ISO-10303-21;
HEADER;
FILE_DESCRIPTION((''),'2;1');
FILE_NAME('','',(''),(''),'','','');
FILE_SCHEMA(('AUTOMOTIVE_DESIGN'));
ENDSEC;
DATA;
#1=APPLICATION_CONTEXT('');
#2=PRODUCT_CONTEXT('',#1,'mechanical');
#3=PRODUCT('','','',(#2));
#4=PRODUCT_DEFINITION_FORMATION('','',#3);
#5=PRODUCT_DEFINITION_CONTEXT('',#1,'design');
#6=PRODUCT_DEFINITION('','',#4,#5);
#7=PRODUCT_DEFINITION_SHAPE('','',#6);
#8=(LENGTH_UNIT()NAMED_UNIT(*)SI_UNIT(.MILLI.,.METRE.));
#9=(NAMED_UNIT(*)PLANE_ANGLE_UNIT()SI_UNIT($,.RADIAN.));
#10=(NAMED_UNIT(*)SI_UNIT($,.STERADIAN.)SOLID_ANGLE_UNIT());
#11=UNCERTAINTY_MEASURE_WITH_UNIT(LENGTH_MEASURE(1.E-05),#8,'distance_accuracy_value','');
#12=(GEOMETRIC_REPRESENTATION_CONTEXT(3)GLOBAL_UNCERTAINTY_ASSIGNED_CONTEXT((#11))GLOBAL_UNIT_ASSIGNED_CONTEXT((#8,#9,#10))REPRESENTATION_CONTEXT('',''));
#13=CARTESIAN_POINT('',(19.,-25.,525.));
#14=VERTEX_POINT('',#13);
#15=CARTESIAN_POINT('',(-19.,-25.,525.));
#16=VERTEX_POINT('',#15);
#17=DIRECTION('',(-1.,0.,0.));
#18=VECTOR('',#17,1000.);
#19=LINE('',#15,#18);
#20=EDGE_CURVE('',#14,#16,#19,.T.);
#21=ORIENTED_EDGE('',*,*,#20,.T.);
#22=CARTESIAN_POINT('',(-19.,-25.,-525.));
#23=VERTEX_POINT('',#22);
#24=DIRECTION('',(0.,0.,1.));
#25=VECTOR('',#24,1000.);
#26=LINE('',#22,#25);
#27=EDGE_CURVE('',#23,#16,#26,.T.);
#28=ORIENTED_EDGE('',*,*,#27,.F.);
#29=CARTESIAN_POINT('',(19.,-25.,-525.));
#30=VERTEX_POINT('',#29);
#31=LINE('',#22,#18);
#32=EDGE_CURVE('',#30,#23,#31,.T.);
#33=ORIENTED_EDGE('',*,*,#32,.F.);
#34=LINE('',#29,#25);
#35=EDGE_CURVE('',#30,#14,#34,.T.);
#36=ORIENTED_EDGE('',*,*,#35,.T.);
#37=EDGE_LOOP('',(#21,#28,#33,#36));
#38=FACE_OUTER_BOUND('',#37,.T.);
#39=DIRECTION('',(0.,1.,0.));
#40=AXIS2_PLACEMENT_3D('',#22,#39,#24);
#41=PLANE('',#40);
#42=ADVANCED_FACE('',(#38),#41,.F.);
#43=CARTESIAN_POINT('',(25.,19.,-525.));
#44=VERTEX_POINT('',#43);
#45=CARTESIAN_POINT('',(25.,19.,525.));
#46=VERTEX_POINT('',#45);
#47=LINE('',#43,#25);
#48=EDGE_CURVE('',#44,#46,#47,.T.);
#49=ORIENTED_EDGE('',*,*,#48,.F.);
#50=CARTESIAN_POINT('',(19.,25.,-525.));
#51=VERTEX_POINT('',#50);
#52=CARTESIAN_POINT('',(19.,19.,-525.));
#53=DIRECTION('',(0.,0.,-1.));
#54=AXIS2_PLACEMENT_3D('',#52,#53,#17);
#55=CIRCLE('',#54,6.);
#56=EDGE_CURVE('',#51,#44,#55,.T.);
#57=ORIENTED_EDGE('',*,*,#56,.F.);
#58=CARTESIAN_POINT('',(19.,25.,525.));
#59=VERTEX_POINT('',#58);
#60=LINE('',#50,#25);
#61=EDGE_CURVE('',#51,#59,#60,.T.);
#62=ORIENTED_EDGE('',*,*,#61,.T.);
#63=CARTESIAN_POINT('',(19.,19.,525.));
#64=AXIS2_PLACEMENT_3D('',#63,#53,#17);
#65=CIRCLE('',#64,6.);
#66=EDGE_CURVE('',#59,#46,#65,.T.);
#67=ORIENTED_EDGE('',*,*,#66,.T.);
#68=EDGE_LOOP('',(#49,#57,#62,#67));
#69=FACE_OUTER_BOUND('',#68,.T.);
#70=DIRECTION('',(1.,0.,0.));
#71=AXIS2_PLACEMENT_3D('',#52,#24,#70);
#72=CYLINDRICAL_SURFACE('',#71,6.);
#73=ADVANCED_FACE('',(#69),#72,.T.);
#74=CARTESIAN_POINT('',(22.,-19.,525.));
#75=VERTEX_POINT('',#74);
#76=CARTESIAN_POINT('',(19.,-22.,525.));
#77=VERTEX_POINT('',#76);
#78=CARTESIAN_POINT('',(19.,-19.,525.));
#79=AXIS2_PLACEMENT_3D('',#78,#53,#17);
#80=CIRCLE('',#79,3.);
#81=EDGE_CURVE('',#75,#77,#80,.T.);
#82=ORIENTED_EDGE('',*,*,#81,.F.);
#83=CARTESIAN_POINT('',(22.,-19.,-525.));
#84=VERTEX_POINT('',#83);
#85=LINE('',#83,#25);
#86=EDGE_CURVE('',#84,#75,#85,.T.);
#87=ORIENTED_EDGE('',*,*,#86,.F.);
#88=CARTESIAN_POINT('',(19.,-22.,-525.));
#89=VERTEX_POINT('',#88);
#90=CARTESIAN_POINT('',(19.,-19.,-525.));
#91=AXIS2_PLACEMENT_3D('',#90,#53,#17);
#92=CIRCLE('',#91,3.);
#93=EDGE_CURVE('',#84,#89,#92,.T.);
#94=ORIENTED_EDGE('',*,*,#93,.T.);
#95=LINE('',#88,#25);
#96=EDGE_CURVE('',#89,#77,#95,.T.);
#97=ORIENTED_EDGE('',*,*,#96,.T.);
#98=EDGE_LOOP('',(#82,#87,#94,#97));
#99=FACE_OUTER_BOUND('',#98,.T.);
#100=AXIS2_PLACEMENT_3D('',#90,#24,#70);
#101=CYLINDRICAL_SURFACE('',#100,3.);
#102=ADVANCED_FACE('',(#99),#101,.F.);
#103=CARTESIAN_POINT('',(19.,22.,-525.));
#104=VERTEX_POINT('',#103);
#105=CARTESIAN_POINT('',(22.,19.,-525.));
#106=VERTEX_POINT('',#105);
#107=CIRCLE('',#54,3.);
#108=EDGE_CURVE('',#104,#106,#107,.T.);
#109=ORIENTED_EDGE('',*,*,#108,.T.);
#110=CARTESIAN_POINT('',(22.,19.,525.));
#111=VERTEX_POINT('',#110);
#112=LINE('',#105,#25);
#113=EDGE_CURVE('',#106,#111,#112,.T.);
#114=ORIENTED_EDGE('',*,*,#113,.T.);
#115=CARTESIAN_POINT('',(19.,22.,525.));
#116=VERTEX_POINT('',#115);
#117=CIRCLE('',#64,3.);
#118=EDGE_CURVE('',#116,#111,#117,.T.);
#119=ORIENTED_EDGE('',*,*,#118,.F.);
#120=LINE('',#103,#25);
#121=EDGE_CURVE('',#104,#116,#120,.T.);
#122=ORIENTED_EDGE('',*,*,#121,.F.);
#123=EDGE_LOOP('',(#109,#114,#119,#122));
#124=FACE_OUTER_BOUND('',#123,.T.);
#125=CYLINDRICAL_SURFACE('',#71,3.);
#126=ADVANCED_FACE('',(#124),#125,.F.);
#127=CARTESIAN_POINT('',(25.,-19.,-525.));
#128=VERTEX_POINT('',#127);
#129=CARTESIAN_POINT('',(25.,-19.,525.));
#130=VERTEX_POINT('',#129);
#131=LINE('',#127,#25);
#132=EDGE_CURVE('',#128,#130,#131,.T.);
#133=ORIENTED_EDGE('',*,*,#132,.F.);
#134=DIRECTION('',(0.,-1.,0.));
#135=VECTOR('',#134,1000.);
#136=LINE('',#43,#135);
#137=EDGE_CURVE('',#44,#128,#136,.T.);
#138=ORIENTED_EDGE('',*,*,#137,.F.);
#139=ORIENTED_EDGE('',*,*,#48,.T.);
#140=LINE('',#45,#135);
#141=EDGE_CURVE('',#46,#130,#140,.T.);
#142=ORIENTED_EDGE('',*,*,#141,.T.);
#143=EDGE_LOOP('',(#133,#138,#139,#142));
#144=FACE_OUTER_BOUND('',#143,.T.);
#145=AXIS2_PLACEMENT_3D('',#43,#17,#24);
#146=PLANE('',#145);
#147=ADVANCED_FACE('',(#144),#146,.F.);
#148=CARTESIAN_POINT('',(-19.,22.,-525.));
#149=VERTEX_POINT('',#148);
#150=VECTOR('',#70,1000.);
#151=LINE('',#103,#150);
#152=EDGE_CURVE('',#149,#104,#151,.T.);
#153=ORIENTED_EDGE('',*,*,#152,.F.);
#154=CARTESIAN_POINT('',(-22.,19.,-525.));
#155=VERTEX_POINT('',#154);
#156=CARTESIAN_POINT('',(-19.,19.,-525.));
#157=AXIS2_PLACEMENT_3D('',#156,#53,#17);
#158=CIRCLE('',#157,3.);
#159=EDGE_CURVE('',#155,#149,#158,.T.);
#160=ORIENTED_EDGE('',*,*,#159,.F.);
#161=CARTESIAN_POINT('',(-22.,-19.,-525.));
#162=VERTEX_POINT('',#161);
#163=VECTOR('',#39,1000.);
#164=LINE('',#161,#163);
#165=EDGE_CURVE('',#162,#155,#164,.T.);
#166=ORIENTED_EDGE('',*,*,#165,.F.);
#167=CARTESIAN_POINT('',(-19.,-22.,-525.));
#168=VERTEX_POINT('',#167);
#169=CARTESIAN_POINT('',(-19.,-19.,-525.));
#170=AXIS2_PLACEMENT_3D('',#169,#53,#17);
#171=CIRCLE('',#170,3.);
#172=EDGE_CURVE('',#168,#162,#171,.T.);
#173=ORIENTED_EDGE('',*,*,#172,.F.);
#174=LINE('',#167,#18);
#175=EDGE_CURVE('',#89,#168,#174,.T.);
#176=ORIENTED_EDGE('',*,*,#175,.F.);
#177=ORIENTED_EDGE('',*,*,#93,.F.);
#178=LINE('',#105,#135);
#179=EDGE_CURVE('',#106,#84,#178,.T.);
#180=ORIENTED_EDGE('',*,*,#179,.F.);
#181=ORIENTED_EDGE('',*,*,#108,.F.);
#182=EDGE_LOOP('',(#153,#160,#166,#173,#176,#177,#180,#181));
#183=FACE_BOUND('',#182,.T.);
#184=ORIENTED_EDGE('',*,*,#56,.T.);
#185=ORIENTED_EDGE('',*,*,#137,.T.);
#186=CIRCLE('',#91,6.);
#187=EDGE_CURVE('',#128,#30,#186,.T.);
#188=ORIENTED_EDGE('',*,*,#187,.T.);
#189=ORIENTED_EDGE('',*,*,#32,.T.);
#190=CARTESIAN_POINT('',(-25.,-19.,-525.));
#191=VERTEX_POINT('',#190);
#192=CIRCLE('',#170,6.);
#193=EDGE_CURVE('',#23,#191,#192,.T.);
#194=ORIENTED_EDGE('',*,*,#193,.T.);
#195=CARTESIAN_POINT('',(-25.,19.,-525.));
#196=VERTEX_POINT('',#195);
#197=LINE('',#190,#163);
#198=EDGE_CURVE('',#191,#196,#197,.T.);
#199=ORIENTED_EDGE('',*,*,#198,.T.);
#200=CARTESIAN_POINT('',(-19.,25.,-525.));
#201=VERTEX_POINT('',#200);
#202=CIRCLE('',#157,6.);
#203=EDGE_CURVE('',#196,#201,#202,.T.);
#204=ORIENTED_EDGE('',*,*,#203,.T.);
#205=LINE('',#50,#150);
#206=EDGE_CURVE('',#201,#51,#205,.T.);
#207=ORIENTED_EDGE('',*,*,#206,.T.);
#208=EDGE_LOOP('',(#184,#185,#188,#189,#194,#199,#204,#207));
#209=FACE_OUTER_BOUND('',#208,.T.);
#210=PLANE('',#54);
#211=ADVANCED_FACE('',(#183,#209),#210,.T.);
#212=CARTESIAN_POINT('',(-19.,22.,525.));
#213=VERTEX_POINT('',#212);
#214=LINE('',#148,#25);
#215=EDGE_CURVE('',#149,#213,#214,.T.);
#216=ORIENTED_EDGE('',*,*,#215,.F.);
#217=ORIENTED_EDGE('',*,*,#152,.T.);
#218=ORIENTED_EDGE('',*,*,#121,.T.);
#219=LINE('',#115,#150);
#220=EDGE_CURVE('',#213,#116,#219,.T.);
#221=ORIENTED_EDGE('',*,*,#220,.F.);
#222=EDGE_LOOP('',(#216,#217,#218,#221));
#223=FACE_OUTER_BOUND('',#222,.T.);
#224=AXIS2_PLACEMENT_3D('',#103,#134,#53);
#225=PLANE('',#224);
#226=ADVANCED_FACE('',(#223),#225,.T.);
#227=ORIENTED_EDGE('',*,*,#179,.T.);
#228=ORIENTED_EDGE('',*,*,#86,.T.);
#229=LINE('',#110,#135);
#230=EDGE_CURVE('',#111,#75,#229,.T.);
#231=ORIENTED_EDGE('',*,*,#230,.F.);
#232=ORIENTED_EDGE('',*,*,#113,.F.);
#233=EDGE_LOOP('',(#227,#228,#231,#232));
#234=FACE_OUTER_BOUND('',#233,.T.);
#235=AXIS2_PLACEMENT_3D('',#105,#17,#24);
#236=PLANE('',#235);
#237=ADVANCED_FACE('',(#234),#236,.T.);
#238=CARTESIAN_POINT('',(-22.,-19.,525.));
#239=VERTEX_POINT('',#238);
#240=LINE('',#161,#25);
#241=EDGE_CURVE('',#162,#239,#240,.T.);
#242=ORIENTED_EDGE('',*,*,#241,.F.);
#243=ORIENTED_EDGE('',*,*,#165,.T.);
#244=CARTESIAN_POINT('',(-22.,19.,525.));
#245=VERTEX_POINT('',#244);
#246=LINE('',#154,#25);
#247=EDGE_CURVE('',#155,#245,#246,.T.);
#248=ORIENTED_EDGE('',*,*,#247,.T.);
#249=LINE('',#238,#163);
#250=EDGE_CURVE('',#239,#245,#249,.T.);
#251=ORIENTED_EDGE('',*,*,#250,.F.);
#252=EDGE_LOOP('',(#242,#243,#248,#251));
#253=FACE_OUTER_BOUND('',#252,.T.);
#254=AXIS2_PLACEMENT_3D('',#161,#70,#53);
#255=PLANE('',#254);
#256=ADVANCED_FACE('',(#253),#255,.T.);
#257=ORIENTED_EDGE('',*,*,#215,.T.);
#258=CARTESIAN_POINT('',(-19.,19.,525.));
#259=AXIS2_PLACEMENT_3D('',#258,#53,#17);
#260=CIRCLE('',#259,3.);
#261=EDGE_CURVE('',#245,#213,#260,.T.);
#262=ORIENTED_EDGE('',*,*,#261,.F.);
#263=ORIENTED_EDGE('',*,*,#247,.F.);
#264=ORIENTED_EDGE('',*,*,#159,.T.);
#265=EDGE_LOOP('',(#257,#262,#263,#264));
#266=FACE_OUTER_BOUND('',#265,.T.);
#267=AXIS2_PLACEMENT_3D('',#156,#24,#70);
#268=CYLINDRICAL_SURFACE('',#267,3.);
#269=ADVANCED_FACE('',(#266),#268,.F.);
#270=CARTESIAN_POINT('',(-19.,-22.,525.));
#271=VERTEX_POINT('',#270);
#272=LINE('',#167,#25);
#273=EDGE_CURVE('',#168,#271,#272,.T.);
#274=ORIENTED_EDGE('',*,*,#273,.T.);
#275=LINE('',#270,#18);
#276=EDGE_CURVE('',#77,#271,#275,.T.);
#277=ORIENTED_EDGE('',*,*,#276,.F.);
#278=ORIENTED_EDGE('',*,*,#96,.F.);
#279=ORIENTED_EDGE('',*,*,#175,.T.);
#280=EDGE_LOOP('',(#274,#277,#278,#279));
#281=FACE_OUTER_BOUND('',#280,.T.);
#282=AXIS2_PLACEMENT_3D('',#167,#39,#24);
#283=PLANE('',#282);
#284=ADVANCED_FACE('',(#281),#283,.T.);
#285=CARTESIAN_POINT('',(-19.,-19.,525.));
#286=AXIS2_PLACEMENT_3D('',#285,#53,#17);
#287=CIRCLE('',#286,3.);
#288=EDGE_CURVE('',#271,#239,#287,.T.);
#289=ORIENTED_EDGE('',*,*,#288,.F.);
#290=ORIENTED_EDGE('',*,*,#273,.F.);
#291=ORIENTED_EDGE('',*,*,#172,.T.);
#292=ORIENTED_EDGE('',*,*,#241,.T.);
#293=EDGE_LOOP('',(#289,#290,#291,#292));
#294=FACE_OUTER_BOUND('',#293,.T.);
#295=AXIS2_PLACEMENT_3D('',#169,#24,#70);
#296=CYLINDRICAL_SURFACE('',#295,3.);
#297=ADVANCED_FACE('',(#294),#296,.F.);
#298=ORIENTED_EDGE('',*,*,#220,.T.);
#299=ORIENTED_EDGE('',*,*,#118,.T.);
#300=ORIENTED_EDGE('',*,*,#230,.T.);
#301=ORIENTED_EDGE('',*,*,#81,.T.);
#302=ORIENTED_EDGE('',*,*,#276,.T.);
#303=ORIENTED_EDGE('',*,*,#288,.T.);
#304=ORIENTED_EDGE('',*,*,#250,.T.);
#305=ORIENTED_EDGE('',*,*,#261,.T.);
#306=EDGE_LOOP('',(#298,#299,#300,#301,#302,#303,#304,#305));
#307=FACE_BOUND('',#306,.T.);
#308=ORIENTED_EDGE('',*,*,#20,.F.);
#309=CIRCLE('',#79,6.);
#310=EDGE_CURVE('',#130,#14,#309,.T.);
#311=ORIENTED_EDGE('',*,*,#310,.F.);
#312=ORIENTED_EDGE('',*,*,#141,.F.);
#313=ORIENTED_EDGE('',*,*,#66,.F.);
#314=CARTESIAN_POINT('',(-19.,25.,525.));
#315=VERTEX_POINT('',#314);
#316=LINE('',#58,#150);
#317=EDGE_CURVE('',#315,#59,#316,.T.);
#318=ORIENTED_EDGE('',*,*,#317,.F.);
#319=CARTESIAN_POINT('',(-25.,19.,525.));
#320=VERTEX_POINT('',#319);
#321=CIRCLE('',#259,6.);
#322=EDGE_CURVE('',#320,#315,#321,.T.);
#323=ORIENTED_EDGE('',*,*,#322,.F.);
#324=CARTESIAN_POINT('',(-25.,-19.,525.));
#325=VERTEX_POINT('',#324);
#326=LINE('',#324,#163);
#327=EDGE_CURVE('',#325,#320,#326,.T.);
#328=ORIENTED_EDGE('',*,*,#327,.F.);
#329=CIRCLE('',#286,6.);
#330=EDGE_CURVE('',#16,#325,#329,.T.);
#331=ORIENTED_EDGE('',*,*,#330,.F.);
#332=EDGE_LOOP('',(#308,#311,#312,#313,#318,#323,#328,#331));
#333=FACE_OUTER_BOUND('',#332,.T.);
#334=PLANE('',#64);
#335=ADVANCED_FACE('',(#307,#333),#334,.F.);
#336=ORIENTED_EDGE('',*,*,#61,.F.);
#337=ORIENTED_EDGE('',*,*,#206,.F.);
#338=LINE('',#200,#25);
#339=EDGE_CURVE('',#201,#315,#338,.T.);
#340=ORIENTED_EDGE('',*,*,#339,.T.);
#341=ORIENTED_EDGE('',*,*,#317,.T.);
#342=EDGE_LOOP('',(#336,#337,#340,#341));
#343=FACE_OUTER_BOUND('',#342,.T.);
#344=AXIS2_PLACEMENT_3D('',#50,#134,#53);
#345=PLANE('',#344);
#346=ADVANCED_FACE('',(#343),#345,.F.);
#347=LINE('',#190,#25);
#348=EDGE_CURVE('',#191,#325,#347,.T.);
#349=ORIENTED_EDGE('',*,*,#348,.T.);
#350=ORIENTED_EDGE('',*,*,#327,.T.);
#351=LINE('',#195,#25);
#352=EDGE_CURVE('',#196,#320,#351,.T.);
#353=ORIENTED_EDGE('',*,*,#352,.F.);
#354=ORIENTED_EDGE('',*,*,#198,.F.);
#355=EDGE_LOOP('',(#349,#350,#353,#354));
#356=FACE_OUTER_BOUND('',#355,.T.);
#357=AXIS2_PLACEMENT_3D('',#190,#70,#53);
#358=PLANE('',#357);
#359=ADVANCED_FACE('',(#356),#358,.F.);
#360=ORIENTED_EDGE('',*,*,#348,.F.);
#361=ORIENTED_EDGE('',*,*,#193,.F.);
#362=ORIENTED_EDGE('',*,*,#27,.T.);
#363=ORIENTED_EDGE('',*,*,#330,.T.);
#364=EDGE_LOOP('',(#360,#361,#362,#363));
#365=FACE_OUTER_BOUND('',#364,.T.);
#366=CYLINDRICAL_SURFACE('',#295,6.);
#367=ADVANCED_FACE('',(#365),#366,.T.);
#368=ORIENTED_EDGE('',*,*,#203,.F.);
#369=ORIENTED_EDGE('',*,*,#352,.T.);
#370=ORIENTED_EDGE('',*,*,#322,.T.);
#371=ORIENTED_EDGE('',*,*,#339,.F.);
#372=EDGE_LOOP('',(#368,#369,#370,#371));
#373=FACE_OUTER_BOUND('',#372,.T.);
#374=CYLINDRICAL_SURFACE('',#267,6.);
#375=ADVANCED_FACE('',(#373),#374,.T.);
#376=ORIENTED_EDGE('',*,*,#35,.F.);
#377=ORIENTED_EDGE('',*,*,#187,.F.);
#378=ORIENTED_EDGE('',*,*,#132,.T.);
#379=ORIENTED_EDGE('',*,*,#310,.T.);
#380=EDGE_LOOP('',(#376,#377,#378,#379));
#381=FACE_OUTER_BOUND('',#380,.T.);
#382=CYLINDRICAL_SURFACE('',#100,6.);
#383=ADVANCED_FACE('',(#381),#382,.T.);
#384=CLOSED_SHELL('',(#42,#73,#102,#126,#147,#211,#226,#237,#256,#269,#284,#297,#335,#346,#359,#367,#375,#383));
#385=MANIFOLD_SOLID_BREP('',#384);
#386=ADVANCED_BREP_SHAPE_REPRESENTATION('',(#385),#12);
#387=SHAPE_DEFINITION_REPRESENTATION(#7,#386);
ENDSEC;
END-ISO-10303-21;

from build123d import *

# Parameters (mm, degrees)
GB_6728_1986_050_X_50_X_3_1_DEPTH = 1050


with BuildPart() as part:
    # Sketch1 → Gb／6728-1986方形空心型钢 050 X 50 X 3(1) (new body)
    with BuildSketch(Plane.YX.offset(-525)):
        with BuildLine():
            Line((-19, -25), (19, -25))
            ThreePointArc((19, -25), (23.242640687, -23.242640687), (25, -19))
            Line((25, -19), (25, 19))
            ThreePointArc((25, 19), (23.242640687, 23.242640687), (19, 25))
            Line((19, 25), (-19, 25))
            ThreePointArc((-19, 25), (-23.242640687, 23.242640687), (-25, 19))
            Line((-25, 19), (-25, -19))
            ThreePointArc((-25, -19), (-23.242640687, -23.242640687), (-19, -25))
        make_face()
        with BuildLine():
            Line((-19, -22), (19, -22))
            ThreePointArc((19, -22), (21.121320344, -21.121320344), (22, -19))
            Line((22, -19), (22, 19))
            ThreePointArc((22, 19), (21.121320344, 21.121320344), (19, 22))
            Line((19, 22), (-19, 22))
            ThreePointArc((-19, 22), (-21.121320344, 21.121320344), (-22, 19))
            Line((-22, 19), (-22, -19))
            ThreePointArc((-22, -19), (-21.121320344, -21.121320344), (-19, -22))
        make_face(mode=Mode.SUBTRACT)
    extrude(amount=GB_6728_1986_050_X_50_X_3_1_DEPTH)


solid = part.part
